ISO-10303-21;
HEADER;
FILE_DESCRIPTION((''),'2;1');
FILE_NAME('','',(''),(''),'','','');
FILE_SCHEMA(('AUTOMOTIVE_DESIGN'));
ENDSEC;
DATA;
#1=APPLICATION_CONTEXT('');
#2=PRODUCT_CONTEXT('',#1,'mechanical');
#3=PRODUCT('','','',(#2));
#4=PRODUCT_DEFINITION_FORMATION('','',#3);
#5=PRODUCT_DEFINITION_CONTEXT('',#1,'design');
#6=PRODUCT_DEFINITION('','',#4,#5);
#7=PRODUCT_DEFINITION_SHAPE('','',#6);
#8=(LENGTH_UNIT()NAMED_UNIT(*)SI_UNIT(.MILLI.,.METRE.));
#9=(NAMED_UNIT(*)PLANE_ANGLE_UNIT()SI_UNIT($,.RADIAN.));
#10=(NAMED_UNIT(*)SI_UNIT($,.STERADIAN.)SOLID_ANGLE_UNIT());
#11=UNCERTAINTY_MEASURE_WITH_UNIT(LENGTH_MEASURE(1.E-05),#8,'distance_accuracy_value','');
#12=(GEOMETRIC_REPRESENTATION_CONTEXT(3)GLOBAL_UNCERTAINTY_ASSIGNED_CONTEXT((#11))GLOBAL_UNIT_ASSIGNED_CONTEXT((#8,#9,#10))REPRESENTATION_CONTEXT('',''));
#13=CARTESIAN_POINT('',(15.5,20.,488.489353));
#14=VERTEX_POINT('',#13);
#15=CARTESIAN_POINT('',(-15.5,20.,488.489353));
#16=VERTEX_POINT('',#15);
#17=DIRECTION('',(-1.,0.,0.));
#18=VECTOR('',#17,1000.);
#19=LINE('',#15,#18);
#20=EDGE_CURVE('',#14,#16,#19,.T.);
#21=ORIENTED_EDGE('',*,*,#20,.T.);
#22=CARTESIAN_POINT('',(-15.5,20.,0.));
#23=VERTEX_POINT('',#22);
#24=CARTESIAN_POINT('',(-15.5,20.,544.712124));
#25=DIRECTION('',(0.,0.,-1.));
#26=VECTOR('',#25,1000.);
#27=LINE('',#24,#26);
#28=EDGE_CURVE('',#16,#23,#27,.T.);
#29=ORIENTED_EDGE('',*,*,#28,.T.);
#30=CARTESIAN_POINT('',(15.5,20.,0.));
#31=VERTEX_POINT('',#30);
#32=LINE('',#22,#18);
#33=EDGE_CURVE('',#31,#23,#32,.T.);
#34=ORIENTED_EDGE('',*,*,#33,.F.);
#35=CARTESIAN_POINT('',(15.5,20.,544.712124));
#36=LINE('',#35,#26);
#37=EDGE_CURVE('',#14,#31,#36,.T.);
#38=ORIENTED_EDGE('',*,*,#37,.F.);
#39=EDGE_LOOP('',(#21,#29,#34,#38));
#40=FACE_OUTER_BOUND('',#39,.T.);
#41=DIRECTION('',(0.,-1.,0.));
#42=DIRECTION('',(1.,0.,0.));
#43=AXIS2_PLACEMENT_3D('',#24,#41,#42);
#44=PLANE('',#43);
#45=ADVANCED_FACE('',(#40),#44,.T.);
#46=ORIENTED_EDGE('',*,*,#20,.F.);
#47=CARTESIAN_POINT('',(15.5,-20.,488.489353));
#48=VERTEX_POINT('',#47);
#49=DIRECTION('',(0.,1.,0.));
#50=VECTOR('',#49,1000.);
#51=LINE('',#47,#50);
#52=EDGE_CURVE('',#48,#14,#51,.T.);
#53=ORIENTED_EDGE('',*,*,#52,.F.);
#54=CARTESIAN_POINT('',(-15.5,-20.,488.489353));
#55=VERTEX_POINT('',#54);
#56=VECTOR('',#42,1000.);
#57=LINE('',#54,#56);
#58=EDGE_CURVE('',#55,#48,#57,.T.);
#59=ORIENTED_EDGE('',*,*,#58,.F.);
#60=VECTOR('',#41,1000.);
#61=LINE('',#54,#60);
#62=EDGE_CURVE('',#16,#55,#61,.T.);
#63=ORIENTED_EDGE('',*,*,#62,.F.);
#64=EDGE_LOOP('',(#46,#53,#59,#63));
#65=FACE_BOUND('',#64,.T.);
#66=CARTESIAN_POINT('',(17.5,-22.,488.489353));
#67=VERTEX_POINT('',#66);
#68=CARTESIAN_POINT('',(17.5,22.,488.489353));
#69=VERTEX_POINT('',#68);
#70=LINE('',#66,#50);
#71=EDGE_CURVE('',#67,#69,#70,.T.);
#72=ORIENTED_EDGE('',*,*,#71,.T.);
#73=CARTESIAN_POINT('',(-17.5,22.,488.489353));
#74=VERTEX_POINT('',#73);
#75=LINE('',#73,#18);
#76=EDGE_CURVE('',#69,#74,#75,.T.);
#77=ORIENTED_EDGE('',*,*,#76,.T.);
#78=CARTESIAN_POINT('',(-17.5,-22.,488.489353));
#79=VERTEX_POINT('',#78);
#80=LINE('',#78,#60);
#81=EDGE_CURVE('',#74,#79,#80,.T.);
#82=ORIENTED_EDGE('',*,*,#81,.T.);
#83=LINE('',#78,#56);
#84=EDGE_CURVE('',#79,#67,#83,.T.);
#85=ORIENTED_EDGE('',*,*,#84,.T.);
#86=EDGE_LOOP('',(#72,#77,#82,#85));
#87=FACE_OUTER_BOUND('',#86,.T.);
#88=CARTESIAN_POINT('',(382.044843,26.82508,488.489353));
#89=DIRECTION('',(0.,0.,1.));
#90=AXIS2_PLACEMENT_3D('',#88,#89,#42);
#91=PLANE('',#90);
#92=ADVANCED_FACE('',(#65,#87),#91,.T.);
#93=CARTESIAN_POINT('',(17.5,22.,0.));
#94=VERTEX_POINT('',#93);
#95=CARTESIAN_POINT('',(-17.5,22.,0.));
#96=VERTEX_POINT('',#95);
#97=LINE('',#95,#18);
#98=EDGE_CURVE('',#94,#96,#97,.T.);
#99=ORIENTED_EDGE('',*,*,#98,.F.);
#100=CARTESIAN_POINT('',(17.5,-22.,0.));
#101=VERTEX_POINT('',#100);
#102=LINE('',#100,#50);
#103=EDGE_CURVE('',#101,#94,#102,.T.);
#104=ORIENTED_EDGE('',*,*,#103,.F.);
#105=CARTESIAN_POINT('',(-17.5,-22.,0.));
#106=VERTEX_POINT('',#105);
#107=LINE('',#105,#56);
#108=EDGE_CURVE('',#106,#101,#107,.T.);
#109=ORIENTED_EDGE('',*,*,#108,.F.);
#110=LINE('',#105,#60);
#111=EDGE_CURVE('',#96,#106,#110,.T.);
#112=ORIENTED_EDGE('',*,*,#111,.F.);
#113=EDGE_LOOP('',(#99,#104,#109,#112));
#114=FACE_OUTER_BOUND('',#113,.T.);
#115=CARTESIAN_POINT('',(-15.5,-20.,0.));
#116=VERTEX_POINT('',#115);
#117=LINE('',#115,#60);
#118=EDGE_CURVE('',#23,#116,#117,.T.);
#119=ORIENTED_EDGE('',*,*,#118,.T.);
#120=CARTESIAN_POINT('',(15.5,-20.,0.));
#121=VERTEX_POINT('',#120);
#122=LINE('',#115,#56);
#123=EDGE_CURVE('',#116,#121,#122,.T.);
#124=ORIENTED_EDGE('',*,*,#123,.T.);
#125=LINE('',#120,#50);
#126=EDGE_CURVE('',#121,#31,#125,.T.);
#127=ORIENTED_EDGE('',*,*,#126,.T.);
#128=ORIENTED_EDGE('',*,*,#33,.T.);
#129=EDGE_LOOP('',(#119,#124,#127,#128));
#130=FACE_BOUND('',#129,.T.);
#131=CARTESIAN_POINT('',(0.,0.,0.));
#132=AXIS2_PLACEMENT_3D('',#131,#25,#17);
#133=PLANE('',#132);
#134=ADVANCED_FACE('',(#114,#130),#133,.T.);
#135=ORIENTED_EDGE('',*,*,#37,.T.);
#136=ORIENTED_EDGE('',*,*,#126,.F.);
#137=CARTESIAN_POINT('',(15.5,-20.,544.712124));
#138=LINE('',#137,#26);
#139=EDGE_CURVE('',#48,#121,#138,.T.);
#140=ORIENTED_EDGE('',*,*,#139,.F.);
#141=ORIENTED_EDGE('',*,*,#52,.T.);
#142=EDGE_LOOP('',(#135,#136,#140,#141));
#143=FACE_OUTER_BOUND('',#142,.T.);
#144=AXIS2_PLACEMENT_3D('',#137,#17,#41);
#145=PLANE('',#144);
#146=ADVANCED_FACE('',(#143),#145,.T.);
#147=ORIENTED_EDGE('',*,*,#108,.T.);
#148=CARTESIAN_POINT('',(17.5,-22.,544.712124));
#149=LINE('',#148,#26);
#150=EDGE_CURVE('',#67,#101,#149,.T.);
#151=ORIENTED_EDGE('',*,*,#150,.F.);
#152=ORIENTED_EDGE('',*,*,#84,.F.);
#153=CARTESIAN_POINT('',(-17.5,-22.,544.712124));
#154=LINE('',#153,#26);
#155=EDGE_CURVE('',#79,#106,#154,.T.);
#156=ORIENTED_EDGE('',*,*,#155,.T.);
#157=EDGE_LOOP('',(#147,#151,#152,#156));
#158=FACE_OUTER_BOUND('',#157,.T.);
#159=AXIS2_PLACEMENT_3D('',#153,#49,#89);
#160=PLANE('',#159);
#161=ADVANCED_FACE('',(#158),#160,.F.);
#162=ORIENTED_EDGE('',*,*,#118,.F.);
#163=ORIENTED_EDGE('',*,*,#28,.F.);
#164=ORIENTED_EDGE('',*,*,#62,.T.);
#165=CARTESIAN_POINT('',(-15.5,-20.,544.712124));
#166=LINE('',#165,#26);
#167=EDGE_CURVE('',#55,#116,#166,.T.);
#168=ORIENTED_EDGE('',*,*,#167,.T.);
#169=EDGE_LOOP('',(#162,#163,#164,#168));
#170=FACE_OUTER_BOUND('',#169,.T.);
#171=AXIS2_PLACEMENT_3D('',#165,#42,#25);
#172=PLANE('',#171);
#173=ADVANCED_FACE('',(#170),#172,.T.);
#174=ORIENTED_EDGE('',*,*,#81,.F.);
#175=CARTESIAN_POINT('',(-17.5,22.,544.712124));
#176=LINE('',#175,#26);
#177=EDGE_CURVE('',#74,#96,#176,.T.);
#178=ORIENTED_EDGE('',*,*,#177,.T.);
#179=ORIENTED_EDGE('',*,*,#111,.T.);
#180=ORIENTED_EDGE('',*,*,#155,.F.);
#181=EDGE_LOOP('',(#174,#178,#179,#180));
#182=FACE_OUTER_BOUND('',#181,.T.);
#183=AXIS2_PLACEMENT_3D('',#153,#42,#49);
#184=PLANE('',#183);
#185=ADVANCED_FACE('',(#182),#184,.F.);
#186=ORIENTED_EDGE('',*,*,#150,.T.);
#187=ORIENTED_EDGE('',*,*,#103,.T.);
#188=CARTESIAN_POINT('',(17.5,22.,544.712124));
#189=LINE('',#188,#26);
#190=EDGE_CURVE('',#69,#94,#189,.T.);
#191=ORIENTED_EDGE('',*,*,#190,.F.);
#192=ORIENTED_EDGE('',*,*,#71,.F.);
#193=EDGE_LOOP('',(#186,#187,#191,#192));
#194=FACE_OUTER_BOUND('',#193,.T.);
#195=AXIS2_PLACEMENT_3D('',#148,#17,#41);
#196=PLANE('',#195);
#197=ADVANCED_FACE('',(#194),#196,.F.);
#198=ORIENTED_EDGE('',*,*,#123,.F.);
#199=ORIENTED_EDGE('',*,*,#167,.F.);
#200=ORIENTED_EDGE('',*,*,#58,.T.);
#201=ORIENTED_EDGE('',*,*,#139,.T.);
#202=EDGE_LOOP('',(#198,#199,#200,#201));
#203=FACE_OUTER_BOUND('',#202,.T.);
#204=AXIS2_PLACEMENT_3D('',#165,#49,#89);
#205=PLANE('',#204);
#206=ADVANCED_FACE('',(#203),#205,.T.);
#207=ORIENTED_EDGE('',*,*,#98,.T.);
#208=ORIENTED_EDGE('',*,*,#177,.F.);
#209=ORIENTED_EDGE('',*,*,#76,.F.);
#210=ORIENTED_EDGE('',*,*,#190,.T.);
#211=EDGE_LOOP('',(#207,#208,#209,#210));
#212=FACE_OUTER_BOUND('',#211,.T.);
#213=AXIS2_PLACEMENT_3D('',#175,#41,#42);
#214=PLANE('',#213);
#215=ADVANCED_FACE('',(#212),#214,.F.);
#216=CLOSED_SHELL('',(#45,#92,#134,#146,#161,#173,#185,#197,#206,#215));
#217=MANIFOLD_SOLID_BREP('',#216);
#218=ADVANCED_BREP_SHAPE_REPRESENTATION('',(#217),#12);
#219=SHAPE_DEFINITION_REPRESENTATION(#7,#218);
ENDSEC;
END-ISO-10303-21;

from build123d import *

# Parameters (mm, degrees)
SKETCH1_W           = 35
SKETCH1_H           = 44
SKETCH1_W_2         = 31
SKETCH1_H_2         = 40
BOSS_EXTRUDE1_DEPTH = 488.48935286


with BuildPart() as part:
    # Sketch1 → Boss-Extrude1 (new body)
    with BuildSketch(Plane.XY):
        Rectangle(SKETCH1_W, SKETCH1_H)
        Rectangle(SKETCH1_W_2, SKETCH1_H_2, mode=Mode.SUBTRACT)
    extrude(amount=BOSS_EXTRUDE1_DEPTH)


solid = part.part
